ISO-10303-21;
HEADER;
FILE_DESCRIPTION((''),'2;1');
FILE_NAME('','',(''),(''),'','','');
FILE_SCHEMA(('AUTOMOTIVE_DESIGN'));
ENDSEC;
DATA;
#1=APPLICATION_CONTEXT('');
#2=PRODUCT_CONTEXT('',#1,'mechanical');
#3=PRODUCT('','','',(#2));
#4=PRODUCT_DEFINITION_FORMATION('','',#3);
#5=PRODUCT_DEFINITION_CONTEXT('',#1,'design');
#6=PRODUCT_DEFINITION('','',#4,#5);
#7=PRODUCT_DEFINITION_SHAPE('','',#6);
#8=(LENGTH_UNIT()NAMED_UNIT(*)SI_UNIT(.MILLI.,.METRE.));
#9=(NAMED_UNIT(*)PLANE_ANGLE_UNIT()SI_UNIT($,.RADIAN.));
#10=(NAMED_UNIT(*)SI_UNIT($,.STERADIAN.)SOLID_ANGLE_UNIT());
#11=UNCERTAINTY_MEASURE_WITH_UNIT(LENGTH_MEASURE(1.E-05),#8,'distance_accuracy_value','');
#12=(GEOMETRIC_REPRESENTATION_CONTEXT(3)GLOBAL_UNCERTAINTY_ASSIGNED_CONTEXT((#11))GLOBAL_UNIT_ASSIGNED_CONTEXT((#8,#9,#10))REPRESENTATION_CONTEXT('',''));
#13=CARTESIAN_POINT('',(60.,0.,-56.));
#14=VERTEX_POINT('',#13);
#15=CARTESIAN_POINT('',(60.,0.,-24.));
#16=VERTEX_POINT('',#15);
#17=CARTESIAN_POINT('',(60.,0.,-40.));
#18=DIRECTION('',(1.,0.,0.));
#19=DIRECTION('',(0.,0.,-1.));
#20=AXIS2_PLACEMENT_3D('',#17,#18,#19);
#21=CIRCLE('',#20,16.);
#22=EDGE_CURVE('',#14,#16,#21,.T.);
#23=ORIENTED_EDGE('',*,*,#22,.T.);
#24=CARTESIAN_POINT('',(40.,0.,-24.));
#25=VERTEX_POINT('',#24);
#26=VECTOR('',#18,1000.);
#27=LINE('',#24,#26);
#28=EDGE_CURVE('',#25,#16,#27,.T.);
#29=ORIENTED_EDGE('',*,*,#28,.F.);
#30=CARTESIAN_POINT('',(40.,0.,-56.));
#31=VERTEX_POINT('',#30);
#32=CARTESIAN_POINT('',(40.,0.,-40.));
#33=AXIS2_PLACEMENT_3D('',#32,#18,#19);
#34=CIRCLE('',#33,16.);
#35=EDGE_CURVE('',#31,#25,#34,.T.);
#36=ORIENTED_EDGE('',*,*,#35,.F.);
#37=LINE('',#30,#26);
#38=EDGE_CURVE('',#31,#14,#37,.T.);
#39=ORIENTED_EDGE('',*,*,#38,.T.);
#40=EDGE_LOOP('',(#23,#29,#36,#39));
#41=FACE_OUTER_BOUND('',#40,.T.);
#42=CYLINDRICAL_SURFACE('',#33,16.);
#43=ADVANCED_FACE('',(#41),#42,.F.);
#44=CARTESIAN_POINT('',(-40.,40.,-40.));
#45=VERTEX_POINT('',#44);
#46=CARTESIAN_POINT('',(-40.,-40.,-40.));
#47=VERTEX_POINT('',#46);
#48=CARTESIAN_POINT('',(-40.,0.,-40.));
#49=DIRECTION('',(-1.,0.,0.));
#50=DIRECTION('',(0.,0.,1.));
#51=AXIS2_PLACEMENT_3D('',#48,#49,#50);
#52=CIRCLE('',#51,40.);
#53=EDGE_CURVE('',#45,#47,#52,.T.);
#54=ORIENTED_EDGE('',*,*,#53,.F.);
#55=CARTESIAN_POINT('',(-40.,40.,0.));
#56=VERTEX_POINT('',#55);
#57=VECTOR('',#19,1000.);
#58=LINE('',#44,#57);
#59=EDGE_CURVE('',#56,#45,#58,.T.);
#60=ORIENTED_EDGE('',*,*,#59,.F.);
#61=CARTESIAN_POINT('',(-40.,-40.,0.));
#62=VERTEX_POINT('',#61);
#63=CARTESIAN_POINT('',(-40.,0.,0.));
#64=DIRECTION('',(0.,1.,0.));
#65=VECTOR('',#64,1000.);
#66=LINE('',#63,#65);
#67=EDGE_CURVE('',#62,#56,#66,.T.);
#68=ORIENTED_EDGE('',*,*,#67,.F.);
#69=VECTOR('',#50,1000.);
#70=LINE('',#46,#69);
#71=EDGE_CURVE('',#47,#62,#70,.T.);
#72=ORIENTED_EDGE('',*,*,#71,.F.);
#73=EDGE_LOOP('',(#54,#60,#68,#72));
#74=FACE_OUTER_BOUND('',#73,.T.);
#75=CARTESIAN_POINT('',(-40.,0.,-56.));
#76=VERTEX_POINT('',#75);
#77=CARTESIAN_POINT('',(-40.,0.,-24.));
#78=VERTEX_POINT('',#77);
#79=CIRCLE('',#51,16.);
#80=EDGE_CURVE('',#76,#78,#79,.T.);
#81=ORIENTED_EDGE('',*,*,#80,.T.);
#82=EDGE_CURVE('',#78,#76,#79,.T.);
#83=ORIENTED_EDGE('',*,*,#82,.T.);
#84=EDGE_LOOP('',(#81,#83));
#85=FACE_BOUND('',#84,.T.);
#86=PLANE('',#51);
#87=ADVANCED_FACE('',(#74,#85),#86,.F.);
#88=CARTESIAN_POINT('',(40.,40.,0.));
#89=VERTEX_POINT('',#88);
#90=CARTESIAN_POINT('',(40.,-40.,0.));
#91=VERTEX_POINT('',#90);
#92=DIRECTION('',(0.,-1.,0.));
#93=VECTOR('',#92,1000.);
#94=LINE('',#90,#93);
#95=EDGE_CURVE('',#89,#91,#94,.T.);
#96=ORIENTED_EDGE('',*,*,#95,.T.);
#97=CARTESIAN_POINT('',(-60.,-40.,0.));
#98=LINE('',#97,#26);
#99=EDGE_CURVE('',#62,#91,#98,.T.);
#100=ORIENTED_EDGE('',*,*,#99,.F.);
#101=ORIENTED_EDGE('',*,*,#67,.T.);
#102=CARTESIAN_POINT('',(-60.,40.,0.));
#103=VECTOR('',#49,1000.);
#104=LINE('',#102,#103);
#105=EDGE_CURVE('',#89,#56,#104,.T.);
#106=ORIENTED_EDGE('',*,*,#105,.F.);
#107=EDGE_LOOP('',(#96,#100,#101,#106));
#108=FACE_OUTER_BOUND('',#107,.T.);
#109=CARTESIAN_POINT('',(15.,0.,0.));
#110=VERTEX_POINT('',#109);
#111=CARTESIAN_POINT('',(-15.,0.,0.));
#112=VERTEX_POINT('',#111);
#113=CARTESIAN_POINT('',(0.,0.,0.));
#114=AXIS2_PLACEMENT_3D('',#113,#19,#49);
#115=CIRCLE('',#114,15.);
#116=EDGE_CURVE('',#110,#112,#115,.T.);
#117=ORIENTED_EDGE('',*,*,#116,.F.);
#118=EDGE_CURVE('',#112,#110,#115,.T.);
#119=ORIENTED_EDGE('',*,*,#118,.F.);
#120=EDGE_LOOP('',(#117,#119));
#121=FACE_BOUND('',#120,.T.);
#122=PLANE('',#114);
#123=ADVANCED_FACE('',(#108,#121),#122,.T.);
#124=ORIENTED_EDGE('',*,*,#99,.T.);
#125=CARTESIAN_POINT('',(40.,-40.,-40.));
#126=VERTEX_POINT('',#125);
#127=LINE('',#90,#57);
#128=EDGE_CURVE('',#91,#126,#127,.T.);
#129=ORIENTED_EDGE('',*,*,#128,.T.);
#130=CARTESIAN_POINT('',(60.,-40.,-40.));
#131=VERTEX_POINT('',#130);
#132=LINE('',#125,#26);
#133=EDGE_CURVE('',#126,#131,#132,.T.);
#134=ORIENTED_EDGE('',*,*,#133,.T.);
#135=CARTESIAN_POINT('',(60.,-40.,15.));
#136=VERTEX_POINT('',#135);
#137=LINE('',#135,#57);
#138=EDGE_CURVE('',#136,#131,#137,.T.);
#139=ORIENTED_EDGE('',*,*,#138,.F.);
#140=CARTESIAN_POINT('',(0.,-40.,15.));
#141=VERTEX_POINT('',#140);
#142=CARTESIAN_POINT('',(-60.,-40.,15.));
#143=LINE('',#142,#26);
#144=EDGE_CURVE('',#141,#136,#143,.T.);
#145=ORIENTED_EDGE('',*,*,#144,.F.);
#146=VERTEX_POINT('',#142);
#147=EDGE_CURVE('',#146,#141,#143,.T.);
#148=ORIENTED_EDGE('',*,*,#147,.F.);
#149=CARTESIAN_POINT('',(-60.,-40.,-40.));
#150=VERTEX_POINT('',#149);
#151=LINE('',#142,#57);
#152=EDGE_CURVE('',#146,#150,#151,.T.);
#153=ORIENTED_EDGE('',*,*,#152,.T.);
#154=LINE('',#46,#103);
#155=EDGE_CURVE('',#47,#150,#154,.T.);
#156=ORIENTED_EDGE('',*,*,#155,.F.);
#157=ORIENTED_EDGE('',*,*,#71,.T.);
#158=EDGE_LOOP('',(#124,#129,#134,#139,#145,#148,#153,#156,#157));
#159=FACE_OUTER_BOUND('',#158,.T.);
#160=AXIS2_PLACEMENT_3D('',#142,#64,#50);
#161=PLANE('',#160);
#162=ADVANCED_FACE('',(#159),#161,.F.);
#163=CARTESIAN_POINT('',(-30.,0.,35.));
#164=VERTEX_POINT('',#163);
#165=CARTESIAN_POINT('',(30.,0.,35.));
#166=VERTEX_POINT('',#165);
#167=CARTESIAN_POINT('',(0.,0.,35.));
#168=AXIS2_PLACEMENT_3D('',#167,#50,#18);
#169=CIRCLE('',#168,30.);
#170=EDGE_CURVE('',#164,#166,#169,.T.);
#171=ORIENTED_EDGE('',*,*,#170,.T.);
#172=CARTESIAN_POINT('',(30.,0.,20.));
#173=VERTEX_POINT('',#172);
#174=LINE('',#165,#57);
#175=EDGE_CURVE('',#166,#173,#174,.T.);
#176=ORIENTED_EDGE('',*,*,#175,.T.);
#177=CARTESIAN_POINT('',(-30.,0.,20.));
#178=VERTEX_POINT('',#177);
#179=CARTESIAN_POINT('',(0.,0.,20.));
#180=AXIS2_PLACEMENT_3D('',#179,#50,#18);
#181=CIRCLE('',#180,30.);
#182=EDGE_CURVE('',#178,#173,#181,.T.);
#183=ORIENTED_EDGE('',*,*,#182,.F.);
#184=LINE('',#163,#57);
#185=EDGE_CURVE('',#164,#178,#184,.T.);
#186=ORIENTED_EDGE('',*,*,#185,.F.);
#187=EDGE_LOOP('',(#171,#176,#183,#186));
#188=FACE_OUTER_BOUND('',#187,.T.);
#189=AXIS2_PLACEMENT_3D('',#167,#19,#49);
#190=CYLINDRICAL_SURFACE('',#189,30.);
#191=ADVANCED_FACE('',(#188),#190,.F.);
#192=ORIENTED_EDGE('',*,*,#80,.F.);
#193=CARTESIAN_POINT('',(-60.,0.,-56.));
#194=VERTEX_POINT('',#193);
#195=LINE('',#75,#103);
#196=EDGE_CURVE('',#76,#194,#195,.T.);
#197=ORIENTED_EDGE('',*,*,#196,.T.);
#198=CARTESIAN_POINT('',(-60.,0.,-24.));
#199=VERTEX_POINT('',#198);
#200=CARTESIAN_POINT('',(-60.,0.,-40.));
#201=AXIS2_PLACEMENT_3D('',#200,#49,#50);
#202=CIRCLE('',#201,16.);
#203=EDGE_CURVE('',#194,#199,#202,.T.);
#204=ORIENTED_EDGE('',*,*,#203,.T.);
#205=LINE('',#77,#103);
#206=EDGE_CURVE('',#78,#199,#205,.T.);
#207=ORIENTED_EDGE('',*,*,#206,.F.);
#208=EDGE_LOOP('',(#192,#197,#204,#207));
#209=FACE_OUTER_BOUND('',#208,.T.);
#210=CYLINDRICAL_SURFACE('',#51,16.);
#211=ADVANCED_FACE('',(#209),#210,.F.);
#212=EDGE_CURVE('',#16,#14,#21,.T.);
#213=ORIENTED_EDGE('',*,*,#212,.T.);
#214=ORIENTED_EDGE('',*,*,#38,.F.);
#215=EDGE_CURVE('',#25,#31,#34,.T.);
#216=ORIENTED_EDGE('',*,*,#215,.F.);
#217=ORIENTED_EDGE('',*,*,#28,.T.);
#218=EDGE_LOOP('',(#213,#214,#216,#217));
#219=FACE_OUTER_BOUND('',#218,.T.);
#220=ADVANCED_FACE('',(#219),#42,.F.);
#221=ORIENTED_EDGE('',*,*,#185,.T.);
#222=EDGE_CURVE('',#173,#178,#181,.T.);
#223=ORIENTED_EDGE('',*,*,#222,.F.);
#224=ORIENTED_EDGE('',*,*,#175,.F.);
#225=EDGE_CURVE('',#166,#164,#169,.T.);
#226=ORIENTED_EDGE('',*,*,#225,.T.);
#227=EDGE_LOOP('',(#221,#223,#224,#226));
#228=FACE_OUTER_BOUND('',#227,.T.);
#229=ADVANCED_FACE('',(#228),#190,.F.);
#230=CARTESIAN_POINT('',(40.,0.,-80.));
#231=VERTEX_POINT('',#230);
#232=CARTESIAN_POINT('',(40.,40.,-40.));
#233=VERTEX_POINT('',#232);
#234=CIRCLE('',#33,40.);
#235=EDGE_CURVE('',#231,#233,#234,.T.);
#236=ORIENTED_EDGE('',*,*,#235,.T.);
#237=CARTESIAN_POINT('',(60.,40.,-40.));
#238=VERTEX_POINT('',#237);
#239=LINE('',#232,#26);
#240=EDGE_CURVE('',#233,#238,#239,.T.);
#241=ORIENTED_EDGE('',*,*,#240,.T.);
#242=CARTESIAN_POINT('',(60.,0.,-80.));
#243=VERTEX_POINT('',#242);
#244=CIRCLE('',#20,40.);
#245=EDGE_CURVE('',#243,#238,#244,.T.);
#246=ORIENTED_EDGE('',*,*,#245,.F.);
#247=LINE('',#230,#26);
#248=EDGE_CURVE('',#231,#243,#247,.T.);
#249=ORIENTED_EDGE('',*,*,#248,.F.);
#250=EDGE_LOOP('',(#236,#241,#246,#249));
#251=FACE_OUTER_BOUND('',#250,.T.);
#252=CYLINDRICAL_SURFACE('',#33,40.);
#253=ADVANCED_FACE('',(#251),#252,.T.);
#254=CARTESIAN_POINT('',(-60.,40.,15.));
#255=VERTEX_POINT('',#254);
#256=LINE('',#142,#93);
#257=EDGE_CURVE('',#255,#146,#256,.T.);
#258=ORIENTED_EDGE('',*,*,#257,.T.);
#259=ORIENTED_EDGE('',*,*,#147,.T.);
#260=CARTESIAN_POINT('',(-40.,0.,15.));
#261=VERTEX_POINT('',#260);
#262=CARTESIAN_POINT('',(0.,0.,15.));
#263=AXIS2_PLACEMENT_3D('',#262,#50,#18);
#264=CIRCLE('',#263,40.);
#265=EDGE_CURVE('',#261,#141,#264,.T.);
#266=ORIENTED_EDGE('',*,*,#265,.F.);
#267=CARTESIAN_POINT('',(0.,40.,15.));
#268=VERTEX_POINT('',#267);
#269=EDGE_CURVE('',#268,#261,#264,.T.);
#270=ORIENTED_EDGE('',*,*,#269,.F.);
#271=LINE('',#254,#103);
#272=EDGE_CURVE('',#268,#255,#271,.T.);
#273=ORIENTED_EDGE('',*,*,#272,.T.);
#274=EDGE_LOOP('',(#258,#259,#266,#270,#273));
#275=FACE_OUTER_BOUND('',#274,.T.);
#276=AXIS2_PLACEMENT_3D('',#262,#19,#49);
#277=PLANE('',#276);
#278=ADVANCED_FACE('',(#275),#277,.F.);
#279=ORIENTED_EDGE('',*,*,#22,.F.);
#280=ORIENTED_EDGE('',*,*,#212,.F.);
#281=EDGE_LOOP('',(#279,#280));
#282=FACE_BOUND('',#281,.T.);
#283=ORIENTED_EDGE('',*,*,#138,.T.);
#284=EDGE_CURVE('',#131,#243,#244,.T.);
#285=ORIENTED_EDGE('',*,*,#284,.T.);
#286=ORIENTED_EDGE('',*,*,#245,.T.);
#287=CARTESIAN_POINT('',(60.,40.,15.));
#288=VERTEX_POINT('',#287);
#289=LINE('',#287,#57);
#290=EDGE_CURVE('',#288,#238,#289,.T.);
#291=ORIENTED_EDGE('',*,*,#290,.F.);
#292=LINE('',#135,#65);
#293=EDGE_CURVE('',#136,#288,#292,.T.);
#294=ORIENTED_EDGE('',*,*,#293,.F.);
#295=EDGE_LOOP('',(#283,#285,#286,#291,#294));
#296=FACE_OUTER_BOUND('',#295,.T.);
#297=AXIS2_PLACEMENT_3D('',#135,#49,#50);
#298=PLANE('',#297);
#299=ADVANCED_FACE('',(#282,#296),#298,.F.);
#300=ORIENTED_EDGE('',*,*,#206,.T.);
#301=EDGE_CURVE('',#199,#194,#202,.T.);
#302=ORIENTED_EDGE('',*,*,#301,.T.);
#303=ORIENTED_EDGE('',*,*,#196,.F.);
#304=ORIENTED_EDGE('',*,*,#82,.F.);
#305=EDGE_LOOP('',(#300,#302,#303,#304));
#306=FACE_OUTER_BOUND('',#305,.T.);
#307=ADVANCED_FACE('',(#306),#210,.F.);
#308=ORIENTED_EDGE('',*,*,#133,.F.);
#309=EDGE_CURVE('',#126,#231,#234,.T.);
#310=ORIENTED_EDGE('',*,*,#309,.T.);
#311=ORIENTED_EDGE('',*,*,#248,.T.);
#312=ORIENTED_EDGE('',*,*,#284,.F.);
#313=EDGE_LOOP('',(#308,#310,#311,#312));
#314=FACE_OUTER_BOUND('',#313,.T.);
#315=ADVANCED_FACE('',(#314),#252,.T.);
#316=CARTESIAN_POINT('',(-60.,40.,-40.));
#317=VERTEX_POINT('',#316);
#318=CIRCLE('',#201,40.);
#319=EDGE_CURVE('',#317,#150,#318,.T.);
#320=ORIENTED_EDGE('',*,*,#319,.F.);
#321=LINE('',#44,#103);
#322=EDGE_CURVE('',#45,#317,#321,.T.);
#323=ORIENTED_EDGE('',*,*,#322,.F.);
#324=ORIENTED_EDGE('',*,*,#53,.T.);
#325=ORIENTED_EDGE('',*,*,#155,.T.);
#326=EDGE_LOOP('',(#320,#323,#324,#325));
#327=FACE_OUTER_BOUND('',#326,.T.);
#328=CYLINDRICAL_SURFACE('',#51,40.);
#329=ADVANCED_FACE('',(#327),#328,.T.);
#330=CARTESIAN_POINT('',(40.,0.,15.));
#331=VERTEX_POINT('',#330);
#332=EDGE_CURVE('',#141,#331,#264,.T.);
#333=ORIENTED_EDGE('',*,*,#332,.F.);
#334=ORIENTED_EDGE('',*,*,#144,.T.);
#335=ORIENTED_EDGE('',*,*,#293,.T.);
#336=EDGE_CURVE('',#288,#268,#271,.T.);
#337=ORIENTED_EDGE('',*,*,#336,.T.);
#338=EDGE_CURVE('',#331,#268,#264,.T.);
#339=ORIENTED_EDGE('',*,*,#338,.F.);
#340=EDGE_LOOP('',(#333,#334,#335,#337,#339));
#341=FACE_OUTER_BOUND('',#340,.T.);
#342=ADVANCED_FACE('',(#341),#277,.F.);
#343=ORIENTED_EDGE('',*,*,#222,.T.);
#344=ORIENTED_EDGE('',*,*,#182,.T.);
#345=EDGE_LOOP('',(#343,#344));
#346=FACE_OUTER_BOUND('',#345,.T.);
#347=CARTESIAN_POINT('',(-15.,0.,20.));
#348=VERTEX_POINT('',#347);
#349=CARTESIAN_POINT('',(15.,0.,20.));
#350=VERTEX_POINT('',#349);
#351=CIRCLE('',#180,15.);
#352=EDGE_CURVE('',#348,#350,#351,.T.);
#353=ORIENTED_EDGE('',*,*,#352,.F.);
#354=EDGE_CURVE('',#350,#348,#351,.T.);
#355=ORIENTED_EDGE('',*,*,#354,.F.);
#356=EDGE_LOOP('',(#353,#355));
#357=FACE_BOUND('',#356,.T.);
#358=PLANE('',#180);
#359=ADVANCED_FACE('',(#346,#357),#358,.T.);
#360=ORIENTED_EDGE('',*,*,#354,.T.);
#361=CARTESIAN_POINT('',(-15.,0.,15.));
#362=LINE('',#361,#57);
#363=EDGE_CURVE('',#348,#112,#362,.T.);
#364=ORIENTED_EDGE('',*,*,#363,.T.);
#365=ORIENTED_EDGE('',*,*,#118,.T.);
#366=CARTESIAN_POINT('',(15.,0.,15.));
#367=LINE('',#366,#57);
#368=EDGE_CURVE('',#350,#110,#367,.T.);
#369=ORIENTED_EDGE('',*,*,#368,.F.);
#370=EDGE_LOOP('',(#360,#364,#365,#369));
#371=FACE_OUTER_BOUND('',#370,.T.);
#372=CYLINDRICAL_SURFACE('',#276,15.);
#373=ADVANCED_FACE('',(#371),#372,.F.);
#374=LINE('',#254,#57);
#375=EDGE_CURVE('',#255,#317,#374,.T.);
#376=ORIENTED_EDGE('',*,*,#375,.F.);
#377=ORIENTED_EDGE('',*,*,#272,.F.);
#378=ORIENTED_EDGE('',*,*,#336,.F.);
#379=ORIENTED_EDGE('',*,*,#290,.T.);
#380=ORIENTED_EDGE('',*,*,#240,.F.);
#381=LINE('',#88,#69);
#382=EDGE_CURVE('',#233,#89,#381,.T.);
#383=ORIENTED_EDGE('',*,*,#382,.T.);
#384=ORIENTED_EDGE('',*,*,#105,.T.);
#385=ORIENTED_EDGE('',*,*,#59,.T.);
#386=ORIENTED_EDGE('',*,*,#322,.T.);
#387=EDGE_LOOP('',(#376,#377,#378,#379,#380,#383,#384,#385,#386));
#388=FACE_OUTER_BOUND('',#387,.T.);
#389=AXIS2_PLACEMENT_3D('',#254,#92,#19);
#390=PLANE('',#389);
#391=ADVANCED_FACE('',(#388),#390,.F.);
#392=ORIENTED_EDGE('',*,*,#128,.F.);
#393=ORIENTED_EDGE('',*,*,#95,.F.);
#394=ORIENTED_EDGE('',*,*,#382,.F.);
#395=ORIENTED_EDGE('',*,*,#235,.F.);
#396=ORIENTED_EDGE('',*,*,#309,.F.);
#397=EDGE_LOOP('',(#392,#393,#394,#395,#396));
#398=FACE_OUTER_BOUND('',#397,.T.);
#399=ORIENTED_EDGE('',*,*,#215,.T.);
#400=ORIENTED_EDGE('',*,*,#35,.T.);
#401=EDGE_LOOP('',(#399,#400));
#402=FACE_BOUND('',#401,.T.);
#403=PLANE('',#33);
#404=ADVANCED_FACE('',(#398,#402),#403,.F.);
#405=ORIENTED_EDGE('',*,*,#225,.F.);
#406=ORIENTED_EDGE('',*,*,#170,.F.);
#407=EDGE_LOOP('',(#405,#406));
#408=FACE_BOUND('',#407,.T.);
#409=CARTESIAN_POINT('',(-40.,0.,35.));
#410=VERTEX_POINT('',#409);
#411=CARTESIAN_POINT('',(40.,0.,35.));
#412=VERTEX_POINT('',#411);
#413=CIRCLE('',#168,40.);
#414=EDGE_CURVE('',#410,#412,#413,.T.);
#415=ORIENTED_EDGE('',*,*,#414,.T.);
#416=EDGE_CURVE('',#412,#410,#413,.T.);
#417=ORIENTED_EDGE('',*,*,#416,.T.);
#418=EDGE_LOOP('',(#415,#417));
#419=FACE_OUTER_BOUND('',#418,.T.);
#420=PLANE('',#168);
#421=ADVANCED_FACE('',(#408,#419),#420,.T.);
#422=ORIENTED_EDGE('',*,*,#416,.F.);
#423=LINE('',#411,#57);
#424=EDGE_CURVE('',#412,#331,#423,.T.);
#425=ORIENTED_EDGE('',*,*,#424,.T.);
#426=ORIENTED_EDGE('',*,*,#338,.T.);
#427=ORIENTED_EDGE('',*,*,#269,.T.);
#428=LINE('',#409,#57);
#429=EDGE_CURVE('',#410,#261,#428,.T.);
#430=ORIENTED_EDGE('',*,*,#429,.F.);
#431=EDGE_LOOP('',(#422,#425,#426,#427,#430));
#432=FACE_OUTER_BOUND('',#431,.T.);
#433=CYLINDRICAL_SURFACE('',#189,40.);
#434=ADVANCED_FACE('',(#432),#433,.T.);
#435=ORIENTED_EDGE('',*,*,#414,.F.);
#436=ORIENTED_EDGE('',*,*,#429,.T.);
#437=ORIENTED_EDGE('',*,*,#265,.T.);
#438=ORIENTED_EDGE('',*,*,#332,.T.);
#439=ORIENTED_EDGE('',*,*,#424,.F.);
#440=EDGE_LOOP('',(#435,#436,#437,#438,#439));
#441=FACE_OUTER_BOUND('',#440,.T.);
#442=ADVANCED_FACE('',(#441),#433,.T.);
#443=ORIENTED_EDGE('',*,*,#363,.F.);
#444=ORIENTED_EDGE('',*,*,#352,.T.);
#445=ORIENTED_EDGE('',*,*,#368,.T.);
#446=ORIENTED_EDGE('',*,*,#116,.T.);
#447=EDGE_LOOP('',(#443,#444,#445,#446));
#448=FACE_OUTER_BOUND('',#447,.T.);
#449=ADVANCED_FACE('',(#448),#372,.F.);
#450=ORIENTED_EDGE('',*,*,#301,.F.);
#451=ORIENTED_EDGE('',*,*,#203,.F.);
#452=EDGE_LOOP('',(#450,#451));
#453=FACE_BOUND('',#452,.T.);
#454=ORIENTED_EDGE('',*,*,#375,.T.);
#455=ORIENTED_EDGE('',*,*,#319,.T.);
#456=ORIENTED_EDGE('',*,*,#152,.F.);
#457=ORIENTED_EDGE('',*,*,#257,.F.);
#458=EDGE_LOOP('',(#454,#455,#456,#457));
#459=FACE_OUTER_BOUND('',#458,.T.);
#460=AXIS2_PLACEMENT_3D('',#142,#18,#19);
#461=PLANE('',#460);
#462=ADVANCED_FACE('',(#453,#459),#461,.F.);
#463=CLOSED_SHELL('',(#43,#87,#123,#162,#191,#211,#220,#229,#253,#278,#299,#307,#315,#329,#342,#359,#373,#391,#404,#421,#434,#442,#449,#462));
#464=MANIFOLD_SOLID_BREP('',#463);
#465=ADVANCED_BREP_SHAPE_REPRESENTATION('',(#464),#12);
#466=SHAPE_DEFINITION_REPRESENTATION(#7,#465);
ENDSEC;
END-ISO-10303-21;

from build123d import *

# Parameters (mm, degrees)
BASE_PLATE_SKETCH_W        = 120
BASE_PLATE_SKETCH_H        = 80
BASE_PLATE_120X80X15_DEPTH = 15
BORE_30_SKETCH_R           = 15
BORE_30_DEPTH              = 15
HUB_BOSS_SKETCH_R          = 40
HUB_BOSS_SKETCH_R_2        = 30
HUB_BOSS_DEPTH             = 20
HUB_INNER_STEP_SKETCH_R    = 30
HUB_INNER_STEP_SKETCH_R_2  = 15
HUB_INNER_STEP_DEPTH       = 5
LUG_A_SKETCH_R             = 16
LUG_A_DEPTH                = 20
LUG_START                  = -20
LUG_B_SKETCH_R             = 16
LUG_B_DEPTH                = 20


with BuildPart() as part:
    # Base Plate Sketch → Base Plate 120x80x15 (new body)
    with BuildSketch(Plane.XY):
        Rectangle(BASE_PLATE_SKETCH_W, BASE_PLATE_SKETCH_H)
    extrude(amount=BASE_PLATE_120X80X15_DEPTH)

    # Bore Ø30 Sketch → Bore Ø30 (cut)
    with BuildSketch(Plane(origin=(0, 0, 0), x_dir=(-1, 0, 0), z_dir=(0, 0, -1))):
        Circle(BORE_30_SKETCH_R)
    extrude(amount=-BORE_30_DEPTH, mode=Mode.SUBTRACT)

    # Hub Boss Sketch → Hub Boss (add)
    with BuildSketch(Plane.XY.offset(15)):
        with Locations(Location((0, 0, 0), (0, 0, 270))):
            Circle(HUB_BOSS_SKETCH_R)
        Circle(HUB_BOSS_SKETCH_R_2, mode=Mode.SUBTRACT)
    extrude(amount=HUB_BOSS_DEPTH)

    # Hub Inner Step Sketch → Hub Inner Step (add)
    with BuildSketch(Plane.XY.offset(15)):
        Circle(HUB_INNER_STEP_SKETCH_R)
        with Locations(Location((0, 0, 0), (0, 0, 180))):
            Circle(HUB_INNER_STEP_SKETCH_R_2, mode=Mode.SUBTRACT)
    extrude(amount=HUB_INNER_STEP_DEPTH)

    # Lug A Sketch → Lug A (add)
    with BuildSketch(Plane(origin=(60, 0, 0), x_dir=(0, 0, -1), z_dir=(1, 0, 0))):
        with BuildLine():
            Line((0, 40), (40, 40))
            ThreePointArc((40, 40), (80, 0), (40, -40))
            Line((40, -40), (0, -40))
            Line((0, -40), (0, 40))
        make_face()
        with Locations((40, 0)):
            Circle(LUG_A_SKETCH_R, mode=Mode.SUBTRACT)
    extrude(amount=-LUG_A_DEPTH)

    # Lug B Sketch → Lug B (add)
    with BuildSketch(Plane.ZY.offset(60).offset(LUG_START)):
        with BuildLine():
            Line((-40, 40), (15, 40))
            Line((15, 40), (15, -40))
            Line((15, -40), (-40, -40))
            ThreePointArc((-40, -40), (-80, 0), (-40, 40))
        make_face()
        with Locations(Location((-40, 0, 0), (0, 0, 180))):
            Circle(LUG_B_SKETCH_R, mode=Mode.SUBTRACT)
    extrude(amount=LUG_B_DEPTH)


solid = part.part
